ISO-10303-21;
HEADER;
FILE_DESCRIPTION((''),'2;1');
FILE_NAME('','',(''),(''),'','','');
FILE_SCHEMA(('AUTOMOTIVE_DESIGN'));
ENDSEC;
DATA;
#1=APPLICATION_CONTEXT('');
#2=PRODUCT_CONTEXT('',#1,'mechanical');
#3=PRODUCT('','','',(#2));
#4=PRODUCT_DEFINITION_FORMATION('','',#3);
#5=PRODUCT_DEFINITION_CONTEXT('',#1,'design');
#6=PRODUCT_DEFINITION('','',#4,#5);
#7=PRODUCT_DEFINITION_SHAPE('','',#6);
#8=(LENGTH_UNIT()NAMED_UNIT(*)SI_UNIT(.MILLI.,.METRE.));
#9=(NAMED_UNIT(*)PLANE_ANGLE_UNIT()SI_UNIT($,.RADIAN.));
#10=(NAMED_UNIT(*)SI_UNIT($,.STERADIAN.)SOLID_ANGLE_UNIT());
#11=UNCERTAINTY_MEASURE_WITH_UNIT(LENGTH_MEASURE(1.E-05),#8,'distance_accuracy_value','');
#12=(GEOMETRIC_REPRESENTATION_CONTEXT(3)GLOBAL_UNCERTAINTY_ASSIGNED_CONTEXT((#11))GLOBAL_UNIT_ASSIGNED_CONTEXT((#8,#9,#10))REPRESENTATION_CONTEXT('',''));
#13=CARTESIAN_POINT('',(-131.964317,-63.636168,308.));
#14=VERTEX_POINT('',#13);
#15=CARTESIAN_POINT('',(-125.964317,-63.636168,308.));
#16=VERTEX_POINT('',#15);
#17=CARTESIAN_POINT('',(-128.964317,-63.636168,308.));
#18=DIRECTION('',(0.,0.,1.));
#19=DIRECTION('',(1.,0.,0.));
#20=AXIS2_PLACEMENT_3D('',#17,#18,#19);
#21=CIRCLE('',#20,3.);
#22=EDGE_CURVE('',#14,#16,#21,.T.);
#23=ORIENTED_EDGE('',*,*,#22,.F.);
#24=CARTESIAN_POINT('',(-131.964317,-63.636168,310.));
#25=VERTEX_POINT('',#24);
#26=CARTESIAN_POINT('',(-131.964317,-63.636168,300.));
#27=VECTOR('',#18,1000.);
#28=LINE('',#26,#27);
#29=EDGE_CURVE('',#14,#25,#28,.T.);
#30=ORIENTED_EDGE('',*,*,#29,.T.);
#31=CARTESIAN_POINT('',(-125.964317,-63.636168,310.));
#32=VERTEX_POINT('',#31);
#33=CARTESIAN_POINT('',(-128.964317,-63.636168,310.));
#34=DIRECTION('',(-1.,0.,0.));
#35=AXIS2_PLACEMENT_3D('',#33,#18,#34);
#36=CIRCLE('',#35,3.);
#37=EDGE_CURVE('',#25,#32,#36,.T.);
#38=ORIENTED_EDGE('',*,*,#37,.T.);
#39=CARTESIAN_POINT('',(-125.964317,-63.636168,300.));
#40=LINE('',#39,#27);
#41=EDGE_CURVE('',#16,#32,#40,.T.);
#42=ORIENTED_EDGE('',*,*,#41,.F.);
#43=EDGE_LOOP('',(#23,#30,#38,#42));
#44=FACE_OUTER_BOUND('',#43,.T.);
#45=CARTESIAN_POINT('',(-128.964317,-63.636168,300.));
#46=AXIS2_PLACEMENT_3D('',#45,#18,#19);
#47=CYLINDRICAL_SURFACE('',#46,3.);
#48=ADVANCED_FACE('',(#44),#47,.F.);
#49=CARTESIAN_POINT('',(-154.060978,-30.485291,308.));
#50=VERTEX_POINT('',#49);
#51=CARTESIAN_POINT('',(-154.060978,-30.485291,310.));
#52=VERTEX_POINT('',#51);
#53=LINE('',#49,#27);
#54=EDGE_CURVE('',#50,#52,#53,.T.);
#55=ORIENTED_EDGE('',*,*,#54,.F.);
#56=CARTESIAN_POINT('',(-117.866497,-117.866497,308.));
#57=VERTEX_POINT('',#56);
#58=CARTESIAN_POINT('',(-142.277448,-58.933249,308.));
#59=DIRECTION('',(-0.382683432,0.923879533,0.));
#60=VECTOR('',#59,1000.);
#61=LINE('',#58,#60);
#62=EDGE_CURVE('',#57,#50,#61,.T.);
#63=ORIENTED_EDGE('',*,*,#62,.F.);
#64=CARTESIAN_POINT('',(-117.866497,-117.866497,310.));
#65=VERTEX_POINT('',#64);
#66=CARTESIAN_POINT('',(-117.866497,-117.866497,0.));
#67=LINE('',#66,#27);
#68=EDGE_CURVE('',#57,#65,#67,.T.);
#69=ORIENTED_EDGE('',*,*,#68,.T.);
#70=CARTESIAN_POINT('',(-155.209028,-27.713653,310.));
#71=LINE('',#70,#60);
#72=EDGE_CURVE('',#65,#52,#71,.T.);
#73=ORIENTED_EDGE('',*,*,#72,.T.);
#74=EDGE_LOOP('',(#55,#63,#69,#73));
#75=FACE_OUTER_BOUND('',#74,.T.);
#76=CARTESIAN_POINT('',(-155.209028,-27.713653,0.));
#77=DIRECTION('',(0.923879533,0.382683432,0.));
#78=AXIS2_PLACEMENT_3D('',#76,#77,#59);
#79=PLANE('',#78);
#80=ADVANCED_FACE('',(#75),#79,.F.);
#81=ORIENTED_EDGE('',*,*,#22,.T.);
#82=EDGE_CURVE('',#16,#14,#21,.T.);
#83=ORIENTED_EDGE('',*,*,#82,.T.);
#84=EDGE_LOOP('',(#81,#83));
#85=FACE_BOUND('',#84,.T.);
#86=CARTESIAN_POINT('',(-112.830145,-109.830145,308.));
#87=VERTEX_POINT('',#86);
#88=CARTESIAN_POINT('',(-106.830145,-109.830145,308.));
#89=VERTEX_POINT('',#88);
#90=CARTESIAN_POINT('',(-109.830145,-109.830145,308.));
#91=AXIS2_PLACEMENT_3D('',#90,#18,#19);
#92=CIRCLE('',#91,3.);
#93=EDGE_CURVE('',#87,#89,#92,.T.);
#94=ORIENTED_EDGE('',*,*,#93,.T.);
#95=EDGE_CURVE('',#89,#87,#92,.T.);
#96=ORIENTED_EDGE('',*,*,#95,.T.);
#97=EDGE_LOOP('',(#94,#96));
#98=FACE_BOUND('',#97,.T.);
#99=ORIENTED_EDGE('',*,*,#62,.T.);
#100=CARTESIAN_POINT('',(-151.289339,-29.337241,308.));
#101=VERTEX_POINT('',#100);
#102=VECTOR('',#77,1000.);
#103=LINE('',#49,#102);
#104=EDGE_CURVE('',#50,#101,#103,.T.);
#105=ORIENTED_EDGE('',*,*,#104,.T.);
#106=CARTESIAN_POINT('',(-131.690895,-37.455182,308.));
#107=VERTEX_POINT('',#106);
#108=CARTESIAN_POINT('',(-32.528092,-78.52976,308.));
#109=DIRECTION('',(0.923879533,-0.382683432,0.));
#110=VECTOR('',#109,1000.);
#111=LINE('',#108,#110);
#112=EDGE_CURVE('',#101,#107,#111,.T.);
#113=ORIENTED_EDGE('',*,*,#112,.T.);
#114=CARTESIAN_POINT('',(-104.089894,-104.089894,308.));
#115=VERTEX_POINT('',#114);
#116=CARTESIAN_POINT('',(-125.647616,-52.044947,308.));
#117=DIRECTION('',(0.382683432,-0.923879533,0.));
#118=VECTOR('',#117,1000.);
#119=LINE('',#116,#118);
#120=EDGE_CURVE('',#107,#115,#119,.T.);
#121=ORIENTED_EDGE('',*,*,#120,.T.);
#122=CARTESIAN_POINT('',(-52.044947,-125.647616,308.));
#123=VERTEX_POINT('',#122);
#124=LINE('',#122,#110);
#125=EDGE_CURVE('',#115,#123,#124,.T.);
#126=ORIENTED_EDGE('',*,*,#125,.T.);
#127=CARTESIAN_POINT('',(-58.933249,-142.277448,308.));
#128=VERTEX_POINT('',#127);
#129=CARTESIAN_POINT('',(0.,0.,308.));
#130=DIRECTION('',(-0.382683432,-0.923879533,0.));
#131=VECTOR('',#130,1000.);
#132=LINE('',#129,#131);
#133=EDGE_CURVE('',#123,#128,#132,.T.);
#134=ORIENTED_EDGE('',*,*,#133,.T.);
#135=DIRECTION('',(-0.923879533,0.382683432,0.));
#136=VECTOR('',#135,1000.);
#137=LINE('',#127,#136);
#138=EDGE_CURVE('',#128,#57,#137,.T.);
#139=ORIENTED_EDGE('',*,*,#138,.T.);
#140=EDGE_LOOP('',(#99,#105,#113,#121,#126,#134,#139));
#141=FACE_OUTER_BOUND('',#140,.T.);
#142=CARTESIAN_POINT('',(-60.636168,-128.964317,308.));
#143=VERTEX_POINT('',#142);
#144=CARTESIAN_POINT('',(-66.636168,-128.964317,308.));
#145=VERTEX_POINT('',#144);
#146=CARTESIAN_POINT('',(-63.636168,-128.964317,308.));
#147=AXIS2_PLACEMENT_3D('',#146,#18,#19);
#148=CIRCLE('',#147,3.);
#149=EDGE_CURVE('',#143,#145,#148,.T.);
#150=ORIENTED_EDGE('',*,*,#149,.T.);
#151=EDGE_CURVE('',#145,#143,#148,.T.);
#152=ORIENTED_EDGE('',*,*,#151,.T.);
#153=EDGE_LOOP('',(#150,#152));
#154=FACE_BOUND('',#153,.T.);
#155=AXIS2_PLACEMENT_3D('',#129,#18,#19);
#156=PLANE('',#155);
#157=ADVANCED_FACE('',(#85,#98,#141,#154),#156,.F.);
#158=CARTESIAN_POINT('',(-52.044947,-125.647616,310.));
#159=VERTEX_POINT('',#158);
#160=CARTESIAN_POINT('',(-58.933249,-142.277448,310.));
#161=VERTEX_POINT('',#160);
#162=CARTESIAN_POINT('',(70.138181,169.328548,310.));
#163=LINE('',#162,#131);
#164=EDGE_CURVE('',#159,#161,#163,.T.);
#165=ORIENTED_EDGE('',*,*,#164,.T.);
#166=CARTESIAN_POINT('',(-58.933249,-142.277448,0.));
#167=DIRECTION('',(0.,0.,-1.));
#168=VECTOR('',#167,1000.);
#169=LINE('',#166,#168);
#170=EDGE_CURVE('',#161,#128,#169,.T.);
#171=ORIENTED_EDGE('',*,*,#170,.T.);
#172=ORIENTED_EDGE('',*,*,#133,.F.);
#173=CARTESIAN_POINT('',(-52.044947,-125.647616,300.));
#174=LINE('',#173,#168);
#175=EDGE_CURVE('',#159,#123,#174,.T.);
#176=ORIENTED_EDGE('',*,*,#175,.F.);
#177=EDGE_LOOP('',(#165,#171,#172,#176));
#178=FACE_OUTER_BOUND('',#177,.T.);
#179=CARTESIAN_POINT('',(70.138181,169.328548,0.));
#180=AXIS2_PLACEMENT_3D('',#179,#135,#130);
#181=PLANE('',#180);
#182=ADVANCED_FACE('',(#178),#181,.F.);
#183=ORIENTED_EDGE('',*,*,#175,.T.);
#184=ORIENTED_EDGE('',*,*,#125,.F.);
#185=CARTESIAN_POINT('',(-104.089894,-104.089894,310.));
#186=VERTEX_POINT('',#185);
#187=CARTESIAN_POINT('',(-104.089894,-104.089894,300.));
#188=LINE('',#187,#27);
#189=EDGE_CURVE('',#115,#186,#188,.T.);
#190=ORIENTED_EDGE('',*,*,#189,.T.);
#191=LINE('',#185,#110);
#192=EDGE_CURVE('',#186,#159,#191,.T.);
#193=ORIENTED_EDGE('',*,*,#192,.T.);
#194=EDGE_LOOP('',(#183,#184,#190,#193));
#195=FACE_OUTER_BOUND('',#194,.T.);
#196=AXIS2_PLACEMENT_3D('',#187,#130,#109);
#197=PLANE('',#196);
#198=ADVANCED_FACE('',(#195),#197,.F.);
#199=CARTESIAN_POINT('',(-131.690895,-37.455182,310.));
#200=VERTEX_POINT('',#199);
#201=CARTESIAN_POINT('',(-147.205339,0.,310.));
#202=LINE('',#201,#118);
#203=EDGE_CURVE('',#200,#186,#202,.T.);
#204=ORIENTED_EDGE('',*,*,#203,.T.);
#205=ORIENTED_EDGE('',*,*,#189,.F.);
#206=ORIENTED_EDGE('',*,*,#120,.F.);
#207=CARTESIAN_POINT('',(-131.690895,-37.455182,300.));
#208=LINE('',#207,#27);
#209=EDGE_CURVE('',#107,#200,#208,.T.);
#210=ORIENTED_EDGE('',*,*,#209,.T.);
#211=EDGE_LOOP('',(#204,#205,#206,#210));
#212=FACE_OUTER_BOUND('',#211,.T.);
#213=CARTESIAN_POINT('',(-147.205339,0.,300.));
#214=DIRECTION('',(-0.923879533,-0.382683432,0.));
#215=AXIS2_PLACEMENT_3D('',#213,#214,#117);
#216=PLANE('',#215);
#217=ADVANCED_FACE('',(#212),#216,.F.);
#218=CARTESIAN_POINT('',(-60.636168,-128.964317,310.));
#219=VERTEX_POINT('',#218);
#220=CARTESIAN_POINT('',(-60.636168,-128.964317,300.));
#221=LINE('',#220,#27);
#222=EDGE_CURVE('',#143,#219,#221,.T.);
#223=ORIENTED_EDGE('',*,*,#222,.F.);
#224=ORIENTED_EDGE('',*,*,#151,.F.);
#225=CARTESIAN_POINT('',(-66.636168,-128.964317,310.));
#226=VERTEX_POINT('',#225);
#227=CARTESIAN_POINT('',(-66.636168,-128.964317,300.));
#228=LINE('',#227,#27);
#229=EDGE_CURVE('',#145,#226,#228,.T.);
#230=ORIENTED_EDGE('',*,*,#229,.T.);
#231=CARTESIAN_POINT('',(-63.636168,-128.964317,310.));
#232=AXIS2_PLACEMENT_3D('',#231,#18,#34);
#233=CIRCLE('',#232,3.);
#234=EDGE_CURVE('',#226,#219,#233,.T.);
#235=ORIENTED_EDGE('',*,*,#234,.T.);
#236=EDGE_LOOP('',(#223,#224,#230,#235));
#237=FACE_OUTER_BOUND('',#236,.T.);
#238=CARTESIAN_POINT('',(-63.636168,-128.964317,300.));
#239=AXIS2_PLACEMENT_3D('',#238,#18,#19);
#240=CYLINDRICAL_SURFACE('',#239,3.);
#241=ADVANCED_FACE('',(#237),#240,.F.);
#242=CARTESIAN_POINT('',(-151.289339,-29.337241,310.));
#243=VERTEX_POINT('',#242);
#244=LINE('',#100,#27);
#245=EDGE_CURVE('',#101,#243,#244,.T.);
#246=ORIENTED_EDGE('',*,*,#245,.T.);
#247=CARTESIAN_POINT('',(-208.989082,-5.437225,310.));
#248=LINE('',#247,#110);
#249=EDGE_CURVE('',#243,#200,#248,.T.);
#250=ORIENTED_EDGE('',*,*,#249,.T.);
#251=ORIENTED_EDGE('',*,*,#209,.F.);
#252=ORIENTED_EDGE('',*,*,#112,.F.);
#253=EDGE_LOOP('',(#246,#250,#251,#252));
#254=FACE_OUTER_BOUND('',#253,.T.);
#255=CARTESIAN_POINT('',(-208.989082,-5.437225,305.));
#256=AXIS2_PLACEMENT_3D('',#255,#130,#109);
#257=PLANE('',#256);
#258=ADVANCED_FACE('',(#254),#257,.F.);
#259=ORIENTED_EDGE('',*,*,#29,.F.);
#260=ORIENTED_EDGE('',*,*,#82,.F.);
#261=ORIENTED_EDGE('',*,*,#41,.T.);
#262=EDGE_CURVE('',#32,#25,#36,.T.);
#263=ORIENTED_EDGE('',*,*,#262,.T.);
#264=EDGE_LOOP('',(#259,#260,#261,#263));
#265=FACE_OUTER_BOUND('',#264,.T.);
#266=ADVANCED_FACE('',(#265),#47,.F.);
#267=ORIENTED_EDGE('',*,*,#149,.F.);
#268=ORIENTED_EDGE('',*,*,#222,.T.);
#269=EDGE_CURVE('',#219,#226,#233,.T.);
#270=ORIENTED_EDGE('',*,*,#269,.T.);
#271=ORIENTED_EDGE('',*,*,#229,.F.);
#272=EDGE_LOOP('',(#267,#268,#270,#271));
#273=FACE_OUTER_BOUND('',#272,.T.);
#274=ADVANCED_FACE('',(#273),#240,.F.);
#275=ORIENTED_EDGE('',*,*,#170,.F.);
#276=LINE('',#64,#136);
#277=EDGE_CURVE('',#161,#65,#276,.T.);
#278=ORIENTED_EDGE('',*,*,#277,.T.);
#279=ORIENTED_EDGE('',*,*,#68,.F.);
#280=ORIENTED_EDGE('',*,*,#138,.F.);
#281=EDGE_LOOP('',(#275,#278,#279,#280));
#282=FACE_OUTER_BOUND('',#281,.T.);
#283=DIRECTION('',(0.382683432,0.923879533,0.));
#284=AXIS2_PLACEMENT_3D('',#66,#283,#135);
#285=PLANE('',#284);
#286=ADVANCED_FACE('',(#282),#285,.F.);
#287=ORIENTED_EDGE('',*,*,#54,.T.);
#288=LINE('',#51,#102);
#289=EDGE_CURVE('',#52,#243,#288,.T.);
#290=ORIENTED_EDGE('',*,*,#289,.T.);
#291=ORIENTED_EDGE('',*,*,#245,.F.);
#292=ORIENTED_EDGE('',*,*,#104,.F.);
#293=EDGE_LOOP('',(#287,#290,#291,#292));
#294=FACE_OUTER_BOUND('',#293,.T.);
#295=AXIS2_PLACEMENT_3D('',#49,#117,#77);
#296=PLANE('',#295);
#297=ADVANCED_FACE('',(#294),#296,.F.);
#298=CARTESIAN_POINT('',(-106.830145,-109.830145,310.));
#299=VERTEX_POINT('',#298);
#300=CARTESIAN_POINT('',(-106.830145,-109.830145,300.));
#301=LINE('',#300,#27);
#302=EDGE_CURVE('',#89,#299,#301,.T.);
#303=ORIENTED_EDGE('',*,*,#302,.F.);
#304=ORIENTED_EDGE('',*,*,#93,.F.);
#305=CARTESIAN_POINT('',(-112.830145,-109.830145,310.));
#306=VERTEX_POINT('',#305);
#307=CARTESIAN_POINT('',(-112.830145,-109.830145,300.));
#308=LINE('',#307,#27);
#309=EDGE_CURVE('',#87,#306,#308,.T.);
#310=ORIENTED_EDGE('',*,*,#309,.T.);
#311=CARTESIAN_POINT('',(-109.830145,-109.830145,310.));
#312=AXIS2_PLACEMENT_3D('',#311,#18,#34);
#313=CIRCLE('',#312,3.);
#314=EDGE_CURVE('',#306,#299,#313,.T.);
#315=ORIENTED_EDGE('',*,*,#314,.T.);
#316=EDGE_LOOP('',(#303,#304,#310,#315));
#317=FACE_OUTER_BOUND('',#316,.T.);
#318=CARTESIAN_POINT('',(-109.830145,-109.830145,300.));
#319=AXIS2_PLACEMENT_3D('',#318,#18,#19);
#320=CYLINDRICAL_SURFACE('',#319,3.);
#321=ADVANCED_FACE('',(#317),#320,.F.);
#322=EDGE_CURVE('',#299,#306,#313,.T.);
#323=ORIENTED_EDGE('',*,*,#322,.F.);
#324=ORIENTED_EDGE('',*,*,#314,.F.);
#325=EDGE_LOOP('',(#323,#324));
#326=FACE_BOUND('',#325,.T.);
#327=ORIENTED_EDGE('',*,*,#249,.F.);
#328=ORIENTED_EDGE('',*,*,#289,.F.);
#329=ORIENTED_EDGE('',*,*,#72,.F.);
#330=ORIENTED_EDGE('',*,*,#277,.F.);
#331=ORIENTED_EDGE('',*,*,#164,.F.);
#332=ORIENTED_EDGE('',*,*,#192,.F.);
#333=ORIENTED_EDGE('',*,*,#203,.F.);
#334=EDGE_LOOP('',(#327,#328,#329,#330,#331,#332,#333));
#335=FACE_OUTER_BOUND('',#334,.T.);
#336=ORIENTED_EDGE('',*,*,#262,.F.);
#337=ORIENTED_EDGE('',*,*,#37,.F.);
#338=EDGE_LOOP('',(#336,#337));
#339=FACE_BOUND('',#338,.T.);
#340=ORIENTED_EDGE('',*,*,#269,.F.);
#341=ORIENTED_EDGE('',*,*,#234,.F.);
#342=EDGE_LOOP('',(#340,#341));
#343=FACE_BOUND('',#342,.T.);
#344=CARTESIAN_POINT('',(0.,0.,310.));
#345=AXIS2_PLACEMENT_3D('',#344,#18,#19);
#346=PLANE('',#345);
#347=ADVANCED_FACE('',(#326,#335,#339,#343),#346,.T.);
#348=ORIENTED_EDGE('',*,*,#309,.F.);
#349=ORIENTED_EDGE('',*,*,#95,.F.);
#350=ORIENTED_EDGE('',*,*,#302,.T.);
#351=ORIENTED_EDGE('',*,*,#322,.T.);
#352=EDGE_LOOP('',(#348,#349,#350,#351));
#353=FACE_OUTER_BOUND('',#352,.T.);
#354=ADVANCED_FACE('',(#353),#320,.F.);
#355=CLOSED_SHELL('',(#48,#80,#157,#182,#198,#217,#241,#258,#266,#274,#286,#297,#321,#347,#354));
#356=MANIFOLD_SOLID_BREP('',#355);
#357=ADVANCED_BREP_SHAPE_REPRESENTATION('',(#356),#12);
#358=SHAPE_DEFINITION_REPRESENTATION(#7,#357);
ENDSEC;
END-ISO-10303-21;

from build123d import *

# Parameters (mm, degrees)
BOSS_EXTRUDE1_DEPTH = 310
SHELL1_T            = -2
CUT_EXTRUDE1_DEPTH  = 10
CUT_EXTRUDE2_DEPTH  = 397.026111511
CUT_EXTRUDE3_DEPTH  = 5
SKETCH5_R           = 3
CUT_EXTRUDE4_DEPTH  = 10
CUT_EXTRUDE5_DEPTH  = 397.026111511
CUT_EXTRUDE7_DEPTH  = 382.100397819
CUT_EXTRUDE8_DEPTH  = 211.562851919


with BuildPart() as part:
    # Sketch1 → Boss-Extrude1 (new body)
    with BuildSketch(Plane.XY):
        Polygon((-174.265144247, 0), (-123.224065222, -123.224065222), (0, -174.265144247), (123.224065222, -123.224065222), (174.265144247, 0), (123.224065222, 123.224065222), (0, 174.265144247), (-123.224065222, 123.224065222), align=None)
    extrude(amount=BOSS_EXTRUDE1_DEPTH)

    # Shell1
    shell1_openings = [part.faces().sort_by_distance(p)[0] for p in [
        (0, 0, 0),
    ]]
    offset(amount=SHELL1_T, openings=shell1_openings, kind=Kind.INTERSECTION)

    # Sketch2 → Cut-Extrude1 (cut)
    with BuildSketch(Plane.XY.offset(310)):
        Polygon((104.089893603, 104.089893603), (0, 147.20533924), (-104.089893603, 104.089893603), (-147.20533924, 0), (-104.089893603, -104.089893603), (0, -147.20533924), (104.089893603, -104.089893603), (147.20533924, 0), align=None)
    extrude(amount=-CUT_EXTRUDE1_DEPTH, mode=Mode.SUBTRACT)

    # Sketch3 → Cut-Extrude2 (cut, through all)
    with BuildSketch(Plane.XY.offset(310)):
        Polygon((70.138181093, 169.328548035), (-63.801020235, -154.029288344), (130.028007017, -234.315900213), (263.967208344, 89.041936166), align=None)
    extrude(amount=-CUT_EXTRUDE2_DEPTH, mode=Mode.SUBTRACT)

    # Sketch4 → Cut-Extrude3 (cut)
    with BuildSketch(Plane.XY.offset(310)):
        Polygon((-143.932898959, 151.622295845), (-51.544945707, 113.353952609), (-116.60112921, -43.705567918), (-208.989082461, -5.437224682), align=None)
    extrude(amount=-CUT_EXTRUDE3_DEPTH, mode=Mode.SUBTRACT)

    # Sketch5 → Cut-Extrude4 (cut)
    with BuildSketch(Plane.XY.offset(310)):
        with Locations((0, 155.323280742)):
            Circle(SKETCH5_R)
        with Locations((-46.193976626, 136.189109124)):
            Circle(SKETCH5_R)
        with Locations((46.193976626, 136.189109124)):
            Circle(SKETCH5_R)
        with Locations((-128.964316707, -63.636168463)):
            Circle(SKETCH5_R)
        with Locations((-109.830145089, -109.830145089)):
            Circle(SKETCH5_R)
        with Locations((-63.636168463, -128.964316707)):
            Circle(SKETCH5_R)
    extrude(amount=-CUT_EXTRUDE4_DEPTH, mode=Mode.SUBTRACT)

    # Sketch19 → Cut-Extrude5 (cut, through all)
    with BuildSketch(Plane.XY.offset(310)):
        Polygon((-32.528091751, -78.529760263), (61.612032611, 148.744604734), (-87.132572124, 210.356637345), (-181.272696485, -16.917727653), align=None)
    extrude(amount=-CUT_EXTRUDE5_DEPTH, mode=Mode.SUBTRACT)

    # Sketch21 → Cut-Extrude7 (cut, through all)
    with BuildSketch(Plane.XY.offset(310)):
        Polygon((-117.866497168, -117.866497168), (-58.933248584, -142.277448007), (-61.612032611, -148.744604734), (-123.224065222, -123.224065222), (-164.354968833, -23.925279891), (-155.209028079, -27.713652592), align=None)
    extrude(amount=-CUT_EXTRUDE7_DEPTH, mode=Mode.SUBTRACT)

    # Sketch22 → Cut-Extrude8 (cut, through all)
    with BuildSketch(Plane.XY.offset(310)):
        Polygon((-154.060977781, -30.48529119), (-155.209028079, -27.713652592), (-151.289339184, -29.337240892), align=None)
    extrude(amount=-CUT_EXTRUDE8_DEPTH, mode=Mode.SUBTRACT)


solid = part.part
